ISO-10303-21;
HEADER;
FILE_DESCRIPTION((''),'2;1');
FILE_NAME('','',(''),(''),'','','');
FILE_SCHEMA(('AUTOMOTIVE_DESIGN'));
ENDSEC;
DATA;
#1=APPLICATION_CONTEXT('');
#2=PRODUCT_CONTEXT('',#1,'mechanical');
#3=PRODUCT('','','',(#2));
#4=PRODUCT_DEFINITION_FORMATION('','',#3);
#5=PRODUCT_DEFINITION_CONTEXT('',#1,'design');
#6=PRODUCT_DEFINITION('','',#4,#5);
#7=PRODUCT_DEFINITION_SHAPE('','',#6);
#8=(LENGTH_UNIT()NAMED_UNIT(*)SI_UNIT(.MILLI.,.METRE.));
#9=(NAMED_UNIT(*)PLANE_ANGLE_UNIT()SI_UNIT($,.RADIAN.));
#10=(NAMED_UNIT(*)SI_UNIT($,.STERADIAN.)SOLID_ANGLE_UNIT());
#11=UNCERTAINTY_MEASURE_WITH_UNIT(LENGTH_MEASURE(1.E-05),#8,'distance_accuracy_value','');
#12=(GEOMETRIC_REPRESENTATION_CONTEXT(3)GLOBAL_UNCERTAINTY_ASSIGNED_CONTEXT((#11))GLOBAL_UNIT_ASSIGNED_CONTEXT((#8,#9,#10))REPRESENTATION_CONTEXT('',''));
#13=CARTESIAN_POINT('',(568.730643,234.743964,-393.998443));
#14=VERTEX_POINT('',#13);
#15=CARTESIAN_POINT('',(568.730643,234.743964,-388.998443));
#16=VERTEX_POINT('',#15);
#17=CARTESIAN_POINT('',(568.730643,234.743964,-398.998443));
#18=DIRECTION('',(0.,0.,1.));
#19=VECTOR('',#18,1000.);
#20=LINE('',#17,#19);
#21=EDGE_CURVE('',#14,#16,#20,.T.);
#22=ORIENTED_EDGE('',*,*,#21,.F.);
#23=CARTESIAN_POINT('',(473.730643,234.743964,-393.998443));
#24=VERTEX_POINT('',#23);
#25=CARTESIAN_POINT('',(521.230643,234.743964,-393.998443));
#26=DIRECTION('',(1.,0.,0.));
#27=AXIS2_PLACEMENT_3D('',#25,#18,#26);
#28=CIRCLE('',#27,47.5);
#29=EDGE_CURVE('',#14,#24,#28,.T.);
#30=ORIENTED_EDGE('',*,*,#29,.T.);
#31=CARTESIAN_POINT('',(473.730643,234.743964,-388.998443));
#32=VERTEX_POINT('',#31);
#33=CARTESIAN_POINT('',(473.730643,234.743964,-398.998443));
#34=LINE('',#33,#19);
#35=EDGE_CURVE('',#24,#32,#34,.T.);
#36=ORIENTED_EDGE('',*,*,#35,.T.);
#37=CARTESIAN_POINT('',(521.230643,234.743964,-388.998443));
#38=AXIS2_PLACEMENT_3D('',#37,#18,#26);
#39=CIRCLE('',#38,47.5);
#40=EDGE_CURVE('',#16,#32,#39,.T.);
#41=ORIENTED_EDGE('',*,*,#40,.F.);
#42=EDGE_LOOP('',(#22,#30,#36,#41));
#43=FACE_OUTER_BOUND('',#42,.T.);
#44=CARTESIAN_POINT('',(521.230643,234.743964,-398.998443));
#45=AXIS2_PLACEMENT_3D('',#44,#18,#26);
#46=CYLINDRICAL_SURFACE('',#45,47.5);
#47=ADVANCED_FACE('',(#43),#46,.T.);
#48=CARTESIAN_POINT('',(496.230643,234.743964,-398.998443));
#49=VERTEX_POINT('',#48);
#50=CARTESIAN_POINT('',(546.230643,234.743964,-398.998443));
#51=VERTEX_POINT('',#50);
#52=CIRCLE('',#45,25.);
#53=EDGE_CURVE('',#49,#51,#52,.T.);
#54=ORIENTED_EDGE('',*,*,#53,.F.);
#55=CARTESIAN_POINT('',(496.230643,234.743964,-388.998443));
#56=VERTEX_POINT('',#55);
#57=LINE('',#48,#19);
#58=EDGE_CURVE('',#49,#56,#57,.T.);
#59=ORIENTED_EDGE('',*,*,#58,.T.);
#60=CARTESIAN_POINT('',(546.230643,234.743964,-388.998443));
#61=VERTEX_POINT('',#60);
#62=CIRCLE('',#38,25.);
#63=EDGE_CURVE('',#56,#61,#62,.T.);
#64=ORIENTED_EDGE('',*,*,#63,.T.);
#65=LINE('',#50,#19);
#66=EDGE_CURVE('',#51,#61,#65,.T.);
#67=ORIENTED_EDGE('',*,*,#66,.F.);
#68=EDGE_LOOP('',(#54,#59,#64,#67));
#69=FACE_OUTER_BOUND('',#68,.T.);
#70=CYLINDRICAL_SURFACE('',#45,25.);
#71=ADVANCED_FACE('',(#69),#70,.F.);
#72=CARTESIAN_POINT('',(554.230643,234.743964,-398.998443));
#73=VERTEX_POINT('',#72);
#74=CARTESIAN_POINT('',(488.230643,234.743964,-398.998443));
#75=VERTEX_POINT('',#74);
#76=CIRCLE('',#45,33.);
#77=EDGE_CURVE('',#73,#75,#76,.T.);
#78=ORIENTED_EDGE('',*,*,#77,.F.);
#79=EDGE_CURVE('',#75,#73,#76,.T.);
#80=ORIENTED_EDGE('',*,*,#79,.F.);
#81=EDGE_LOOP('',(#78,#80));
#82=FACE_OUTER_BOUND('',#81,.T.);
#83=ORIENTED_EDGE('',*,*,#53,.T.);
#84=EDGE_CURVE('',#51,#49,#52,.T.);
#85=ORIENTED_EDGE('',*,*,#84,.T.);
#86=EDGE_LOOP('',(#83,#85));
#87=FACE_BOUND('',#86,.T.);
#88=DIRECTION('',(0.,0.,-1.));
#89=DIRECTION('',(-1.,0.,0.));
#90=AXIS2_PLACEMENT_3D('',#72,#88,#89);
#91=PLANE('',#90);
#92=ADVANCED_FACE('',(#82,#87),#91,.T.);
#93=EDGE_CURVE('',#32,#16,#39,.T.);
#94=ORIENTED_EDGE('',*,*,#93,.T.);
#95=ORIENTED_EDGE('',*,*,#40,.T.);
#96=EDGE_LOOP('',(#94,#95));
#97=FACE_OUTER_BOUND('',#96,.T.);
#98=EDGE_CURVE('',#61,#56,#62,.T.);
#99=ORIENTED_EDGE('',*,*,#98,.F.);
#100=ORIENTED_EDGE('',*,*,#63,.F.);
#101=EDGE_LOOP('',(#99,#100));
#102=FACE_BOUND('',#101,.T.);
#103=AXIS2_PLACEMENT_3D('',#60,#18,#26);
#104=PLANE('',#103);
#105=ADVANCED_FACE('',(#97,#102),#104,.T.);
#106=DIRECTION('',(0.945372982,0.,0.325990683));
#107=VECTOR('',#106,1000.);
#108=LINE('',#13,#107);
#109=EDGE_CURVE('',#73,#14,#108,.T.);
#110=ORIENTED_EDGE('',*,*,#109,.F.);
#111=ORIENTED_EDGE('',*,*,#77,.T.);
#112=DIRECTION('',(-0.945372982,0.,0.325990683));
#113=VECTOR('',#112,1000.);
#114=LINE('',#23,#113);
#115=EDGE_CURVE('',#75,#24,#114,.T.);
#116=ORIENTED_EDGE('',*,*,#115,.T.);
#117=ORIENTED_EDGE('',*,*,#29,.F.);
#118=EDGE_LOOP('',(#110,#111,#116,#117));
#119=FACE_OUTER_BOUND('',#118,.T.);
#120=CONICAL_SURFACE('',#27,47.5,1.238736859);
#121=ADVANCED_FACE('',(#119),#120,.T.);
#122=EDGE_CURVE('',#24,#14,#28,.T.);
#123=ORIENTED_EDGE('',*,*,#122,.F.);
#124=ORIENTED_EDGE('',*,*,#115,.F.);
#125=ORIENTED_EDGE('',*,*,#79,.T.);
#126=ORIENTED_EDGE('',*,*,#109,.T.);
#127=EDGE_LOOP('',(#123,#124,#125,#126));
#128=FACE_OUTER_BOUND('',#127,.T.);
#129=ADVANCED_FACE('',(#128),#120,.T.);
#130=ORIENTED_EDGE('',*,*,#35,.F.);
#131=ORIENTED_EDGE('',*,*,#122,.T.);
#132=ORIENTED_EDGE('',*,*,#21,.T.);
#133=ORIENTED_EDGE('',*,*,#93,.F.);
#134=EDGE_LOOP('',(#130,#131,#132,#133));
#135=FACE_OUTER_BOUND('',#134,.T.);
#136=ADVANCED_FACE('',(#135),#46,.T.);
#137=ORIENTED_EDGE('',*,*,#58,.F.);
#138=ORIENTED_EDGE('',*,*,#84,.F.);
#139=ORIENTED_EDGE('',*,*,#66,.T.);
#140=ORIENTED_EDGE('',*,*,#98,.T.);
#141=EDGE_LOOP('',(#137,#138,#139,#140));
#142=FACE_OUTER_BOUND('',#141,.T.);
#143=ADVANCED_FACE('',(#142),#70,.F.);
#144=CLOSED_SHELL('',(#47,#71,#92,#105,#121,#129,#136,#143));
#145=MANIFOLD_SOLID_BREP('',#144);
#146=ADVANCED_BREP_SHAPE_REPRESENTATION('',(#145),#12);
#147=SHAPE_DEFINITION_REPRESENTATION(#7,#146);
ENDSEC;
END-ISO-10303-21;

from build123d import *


with BuildPart() as part:
    # Sketch1 → Revolve1 (revolve)
    with BuildSketch(Plane(origin=(0, 234.743963655, 0), x_dir=(1, 0, 0), z_dir=(0, 1, 0))):
        Polygon((546.230642584, 388.998443067), (568.730642584, 388.998443067), (568.730642584, 393.998443067), (554.230642584, 398.998443067), (546.230642584, 398.998443067), align=None)
    revolve(axis=Axis((521.230642584, 234.743963655, -398.998443067), (0, 0, 1)))


solid = part.part
